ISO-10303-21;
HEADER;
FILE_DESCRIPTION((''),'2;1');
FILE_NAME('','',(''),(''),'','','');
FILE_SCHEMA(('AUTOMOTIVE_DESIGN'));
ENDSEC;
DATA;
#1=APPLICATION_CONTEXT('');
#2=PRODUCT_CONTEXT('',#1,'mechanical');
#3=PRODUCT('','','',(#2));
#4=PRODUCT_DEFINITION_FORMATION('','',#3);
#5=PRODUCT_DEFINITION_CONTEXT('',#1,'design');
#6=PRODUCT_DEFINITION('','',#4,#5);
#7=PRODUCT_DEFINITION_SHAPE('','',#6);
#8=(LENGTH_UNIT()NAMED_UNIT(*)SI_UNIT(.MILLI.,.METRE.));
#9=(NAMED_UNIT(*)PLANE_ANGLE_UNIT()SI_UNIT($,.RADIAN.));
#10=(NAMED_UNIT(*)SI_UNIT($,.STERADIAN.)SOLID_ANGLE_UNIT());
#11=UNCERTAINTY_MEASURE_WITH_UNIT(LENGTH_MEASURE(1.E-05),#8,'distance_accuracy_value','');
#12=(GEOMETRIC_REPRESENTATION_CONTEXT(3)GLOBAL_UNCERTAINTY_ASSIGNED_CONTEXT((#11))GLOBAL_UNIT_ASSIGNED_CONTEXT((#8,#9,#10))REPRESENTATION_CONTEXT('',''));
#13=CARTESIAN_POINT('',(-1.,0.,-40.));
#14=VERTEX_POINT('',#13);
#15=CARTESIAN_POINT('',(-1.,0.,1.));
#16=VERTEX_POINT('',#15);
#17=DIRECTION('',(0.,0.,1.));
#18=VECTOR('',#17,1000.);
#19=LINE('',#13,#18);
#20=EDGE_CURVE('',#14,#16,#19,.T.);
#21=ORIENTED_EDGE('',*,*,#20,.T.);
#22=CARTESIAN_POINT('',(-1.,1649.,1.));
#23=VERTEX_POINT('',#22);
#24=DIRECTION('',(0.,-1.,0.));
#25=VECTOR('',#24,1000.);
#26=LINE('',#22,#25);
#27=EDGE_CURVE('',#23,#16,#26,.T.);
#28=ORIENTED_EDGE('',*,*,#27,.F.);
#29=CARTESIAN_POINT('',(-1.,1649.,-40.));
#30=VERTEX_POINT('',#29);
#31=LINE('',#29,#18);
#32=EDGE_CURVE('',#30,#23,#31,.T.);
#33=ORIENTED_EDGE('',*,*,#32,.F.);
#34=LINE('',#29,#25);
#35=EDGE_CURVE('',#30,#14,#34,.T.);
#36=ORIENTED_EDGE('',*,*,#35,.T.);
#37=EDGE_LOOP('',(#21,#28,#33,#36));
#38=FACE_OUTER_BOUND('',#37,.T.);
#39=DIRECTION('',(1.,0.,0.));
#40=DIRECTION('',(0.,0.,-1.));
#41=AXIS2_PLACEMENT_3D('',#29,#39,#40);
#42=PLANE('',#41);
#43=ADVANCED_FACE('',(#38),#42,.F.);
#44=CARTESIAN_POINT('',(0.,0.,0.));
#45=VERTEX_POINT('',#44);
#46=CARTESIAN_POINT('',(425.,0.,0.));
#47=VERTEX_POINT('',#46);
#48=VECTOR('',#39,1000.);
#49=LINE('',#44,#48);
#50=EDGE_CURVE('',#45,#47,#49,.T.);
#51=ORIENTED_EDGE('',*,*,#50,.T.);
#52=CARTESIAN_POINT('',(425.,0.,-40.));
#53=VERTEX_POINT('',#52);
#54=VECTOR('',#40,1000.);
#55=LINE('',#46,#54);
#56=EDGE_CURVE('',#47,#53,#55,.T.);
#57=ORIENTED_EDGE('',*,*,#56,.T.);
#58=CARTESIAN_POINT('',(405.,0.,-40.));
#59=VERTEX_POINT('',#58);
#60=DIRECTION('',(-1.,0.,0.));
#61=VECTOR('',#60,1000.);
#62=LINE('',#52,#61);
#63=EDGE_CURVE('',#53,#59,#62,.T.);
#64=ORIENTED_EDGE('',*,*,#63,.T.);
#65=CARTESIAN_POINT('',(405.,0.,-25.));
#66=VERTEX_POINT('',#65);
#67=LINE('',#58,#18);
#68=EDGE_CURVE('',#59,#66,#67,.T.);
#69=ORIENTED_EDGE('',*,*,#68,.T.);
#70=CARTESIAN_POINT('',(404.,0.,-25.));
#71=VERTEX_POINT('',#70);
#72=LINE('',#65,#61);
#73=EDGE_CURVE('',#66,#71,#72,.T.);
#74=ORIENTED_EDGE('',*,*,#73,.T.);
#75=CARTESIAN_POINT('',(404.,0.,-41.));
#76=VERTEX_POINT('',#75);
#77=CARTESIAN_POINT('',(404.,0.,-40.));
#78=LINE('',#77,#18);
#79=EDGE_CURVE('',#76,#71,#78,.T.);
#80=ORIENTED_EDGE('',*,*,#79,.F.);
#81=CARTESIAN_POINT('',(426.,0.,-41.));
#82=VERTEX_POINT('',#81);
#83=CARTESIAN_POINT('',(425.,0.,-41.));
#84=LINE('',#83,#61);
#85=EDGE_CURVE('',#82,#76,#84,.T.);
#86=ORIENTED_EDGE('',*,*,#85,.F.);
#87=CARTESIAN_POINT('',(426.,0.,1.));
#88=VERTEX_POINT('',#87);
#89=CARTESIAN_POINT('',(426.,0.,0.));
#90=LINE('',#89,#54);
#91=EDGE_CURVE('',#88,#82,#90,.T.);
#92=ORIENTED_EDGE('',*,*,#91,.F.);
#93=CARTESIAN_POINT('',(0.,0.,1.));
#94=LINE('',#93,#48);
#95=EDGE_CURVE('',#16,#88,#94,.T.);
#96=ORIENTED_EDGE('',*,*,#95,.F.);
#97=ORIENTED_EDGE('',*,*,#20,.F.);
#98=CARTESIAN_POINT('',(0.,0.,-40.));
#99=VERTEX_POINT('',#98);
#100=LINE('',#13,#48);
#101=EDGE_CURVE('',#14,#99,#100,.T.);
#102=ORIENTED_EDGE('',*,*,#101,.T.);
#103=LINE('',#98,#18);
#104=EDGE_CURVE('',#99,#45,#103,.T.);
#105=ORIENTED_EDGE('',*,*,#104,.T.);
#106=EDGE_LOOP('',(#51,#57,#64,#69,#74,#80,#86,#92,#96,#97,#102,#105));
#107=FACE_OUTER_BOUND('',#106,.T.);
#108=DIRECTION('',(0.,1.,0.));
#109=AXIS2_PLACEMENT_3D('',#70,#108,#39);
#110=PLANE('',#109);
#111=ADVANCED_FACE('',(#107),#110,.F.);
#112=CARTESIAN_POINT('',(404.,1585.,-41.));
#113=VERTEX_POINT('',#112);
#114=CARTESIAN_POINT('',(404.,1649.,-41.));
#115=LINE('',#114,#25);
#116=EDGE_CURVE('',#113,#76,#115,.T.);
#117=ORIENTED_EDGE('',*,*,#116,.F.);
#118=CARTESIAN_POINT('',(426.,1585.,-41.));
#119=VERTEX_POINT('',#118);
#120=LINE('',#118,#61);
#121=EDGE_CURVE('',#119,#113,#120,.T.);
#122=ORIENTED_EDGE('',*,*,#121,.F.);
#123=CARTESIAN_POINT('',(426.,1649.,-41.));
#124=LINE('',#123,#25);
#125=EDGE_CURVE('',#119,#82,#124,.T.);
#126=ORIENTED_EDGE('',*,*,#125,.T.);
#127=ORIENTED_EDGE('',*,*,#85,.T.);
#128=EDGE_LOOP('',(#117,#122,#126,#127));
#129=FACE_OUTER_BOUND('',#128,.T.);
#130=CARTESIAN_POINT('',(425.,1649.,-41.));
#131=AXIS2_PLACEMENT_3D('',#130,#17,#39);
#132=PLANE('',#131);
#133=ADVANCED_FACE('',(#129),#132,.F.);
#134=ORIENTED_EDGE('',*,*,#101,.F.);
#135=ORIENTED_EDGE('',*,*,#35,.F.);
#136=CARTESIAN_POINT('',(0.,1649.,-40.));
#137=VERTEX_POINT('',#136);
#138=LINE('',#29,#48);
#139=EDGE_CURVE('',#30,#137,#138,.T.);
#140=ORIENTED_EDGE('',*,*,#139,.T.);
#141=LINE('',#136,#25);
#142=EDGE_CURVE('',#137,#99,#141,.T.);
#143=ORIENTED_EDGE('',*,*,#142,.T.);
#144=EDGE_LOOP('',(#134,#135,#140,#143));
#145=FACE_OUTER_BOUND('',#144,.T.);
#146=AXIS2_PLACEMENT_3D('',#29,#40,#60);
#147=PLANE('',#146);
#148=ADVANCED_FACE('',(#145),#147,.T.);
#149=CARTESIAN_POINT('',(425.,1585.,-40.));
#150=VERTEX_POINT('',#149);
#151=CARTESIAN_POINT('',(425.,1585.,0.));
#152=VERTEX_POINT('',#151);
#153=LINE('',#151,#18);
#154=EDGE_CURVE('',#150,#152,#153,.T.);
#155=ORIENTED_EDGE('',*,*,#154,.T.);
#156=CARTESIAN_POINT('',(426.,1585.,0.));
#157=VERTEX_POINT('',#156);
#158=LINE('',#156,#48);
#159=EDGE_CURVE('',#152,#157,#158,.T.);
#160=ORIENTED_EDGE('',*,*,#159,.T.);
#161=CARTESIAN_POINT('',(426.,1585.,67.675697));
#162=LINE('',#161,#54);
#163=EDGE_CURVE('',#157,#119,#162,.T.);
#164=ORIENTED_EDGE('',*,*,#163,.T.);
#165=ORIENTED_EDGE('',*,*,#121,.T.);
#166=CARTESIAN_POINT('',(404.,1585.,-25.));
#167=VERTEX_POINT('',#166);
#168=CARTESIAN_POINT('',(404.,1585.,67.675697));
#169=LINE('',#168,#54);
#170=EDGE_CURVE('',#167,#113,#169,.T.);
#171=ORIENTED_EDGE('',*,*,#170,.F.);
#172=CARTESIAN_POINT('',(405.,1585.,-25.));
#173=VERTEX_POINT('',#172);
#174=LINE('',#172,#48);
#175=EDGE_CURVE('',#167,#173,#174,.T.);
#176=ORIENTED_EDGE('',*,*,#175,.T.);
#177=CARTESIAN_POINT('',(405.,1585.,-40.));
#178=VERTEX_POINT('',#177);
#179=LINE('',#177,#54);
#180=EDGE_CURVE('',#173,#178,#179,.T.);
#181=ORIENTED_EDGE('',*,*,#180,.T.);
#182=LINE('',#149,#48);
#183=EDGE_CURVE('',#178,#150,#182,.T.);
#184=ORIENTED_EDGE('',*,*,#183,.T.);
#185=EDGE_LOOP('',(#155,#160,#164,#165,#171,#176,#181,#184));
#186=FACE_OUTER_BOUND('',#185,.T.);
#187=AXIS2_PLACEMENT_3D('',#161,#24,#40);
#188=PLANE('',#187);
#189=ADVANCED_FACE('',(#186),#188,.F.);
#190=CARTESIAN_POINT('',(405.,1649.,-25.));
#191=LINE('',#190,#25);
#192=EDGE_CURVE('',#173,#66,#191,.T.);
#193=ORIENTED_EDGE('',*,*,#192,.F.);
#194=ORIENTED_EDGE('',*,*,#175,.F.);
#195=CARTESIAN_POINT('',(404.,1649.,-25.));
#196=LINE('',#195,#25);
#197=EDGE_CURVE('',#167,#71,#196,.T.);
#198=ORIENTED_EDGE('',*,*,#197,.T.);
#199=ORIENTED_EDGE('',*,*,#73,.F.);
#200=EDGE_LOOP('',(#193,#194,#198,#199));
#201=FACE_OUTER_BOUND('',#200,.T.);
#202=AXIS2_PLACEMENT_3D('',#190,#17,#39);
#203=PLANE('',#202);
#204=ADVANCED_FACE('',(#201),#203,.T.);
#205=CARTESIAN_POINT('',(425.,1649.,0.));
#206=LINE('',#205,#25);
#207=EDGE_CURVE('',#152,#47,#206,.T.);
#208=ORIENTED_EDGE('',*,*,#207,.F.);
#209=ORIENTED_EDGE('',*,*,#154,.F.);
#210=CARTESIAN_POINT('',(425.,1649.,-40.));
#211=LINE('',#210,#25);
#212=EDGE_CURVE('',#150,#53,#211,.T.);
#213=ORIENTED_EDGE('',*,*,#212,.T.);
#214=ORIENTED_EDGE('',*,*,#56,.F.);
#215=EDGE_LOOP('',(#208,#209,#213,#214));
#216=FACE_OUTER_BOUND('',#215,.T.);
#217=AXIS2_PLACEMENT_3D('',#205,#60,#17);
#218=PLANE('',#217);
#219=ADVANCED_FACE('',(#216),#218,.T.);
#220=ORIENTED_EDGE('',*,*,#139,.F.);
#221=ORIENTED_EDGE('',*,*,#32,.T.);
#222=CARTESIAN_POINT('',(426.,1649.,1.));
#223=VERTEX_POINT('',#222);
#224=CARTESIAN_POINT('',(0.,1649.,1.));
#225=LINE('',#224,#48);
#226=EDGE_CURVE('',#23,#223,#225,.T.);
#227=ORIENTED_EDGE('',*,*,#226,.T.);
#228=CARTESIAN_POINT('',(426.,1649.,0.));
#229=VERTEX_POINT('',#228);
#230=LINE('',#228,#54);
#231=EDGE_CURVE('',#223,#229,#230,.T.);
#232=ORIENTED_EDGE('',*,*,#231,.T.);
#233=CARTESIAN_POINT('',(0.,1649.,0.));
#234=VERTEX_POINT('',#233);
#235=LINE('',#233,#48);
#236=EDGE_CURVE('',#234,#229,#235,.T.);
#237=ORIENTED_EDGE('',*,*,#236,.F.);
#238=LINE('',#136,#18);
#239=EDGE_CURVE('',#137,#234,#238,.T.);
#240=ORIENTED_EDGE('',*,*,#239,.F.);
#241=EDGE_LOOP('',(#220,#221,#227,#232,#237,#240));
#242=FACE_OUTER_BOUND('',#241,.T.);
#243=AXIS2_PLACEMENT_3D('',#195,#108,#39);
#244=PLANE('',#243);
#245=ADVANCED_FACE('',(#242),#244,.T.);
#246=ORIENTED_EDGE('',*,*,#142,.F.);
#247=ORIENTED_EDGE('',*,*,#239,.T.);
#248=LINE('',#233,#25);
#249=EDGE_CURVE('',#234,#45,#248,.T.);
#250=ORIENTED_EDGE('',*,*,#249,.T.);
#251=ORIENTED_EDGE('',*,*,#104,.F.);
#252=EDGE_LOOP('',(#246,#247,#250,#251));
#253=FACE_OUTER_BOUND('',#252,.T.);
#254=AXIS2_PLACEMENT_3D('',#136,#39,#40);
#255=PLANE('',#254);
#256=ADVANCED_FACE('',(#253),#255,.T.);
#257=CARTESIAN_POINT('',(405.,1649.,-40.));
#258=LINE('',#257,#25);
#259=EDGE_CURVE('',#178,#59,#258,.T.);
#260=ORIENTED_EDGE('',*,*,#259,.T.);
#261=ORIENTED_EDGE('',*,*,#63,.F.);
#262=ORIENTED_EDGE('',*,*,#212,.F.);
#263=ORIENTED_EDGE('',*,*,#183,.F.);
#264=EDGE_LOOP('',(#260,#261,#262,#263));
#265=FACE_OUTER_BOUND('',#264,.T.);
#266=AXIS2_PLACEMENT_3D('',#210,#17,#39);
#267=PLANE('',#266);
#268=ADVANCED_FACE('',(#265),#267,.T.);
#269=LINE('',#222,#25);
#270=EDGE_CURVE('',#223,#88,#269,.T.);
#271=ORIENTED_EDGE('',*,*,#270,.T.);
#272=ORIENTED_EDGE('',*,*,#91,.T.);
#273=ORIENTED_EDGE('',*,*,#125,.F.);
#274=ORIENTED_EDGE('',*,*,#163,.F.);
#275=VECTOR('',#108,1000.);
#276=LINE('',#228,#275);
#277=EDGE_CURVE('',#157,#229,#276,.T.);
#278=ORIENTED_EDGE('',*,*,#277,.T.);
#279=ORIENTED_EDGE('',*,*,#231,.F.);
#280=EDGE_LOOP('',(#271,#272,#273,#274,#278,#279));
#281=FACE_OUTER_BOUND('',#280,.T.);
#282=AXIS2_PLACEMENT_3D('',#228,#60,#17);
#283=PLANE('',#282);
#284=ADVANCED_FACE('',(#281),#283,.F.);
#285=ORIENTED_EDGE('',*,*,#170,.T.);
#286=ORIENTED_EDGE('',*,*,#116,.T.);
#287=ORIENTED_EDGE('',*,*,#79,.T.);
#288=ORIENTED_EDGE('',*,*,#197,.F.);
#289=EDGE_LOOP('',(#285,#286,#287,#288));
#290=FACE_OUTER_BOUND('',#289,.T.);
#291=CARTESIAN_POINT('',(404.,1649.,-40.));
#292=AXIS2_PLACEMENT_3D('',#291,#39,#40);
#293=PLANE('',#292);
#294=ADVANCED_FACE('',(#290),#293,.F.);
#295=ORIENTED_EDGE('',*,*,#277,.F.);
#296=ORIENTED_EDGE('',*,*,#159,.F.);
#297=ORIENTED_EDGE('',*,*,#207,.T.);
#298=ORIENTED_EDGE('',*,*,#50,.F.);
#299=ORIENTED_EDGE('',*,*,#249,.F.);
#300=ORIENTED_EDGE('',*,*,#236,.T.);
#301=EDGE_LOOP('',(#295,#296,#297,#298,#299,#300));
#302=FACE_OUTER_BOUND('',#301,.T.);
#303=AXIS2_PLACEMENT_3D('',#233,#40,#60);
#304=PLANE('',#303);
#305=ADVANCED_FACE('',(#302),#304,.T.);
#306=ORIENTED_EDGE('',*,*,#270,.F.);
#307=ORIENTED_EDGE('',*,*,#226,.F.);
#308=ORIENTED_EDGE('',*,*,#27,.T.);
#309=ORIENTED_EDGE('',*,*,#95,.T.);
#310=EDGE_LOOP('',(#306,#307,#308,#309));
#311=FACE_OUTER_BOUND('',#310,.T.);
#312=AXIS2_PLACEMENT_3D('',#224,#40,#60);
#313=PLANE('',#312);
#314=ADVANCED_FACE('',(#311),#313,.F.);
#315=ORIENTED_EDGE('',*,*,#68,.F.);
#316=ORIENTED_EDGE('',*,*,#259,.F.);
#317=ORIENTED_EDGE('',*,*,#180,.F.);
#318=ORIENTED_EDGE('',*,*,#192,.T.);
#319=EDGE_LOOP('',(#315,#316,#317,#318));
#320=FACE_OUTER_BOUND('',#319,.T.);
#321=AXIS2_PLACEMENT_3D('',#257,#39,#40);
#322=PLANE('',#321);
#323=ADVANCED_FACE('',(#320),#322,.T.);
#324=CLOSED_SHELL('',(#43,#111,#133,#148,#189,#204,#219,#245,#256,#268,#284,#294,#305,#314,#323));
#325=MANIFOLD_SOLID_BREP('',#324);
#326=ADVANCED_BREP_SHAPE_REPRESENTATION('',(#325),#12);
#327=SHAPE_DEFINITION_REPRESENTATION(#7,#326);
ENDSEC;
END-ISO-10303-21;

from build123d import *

# Parameters (mm, degrees)
EXTRUDE_THIN1_DEPTH = 1649
SKETCH4_W           = 22
SKETCH4_H           = 64
CUT_EXTRUDE1_DEPTH  = 41


with BuildPart() as part:
    # Sketch3 → Extrude-Thin1 (new body)
    with BuildSketch(Plane(origin=(0, 0, 0), x_dir=(1, 0, 0), z_dir=(0, 1, 0))):
        Polygon((0, 40), (0, 0), (425, 0), (425, 40), (405, 40), (405, 25), (404, 25), (404, 41), (426, 41), (426, -1), (-1, -1), (-1, 40), align=None)
    extrude(amount=EXTRUDE_THIN1_DEPTH)

    # Sketch4 → Cut-Extrude1 (cut)
    with BuildSketch(Plane(origin=(0, 0, -41), x_dir=(-1, 0, 0), z_dir=(0, 0, -1))):
        with Locations((-415, 1617)):
            Rectangle(SKETCH4_W, SKETCH4_H)
    extrude(amount=-CUT_EXTRUDE1_DEPTH, mode=Mode.SUBTRACT)


solid = part.part
